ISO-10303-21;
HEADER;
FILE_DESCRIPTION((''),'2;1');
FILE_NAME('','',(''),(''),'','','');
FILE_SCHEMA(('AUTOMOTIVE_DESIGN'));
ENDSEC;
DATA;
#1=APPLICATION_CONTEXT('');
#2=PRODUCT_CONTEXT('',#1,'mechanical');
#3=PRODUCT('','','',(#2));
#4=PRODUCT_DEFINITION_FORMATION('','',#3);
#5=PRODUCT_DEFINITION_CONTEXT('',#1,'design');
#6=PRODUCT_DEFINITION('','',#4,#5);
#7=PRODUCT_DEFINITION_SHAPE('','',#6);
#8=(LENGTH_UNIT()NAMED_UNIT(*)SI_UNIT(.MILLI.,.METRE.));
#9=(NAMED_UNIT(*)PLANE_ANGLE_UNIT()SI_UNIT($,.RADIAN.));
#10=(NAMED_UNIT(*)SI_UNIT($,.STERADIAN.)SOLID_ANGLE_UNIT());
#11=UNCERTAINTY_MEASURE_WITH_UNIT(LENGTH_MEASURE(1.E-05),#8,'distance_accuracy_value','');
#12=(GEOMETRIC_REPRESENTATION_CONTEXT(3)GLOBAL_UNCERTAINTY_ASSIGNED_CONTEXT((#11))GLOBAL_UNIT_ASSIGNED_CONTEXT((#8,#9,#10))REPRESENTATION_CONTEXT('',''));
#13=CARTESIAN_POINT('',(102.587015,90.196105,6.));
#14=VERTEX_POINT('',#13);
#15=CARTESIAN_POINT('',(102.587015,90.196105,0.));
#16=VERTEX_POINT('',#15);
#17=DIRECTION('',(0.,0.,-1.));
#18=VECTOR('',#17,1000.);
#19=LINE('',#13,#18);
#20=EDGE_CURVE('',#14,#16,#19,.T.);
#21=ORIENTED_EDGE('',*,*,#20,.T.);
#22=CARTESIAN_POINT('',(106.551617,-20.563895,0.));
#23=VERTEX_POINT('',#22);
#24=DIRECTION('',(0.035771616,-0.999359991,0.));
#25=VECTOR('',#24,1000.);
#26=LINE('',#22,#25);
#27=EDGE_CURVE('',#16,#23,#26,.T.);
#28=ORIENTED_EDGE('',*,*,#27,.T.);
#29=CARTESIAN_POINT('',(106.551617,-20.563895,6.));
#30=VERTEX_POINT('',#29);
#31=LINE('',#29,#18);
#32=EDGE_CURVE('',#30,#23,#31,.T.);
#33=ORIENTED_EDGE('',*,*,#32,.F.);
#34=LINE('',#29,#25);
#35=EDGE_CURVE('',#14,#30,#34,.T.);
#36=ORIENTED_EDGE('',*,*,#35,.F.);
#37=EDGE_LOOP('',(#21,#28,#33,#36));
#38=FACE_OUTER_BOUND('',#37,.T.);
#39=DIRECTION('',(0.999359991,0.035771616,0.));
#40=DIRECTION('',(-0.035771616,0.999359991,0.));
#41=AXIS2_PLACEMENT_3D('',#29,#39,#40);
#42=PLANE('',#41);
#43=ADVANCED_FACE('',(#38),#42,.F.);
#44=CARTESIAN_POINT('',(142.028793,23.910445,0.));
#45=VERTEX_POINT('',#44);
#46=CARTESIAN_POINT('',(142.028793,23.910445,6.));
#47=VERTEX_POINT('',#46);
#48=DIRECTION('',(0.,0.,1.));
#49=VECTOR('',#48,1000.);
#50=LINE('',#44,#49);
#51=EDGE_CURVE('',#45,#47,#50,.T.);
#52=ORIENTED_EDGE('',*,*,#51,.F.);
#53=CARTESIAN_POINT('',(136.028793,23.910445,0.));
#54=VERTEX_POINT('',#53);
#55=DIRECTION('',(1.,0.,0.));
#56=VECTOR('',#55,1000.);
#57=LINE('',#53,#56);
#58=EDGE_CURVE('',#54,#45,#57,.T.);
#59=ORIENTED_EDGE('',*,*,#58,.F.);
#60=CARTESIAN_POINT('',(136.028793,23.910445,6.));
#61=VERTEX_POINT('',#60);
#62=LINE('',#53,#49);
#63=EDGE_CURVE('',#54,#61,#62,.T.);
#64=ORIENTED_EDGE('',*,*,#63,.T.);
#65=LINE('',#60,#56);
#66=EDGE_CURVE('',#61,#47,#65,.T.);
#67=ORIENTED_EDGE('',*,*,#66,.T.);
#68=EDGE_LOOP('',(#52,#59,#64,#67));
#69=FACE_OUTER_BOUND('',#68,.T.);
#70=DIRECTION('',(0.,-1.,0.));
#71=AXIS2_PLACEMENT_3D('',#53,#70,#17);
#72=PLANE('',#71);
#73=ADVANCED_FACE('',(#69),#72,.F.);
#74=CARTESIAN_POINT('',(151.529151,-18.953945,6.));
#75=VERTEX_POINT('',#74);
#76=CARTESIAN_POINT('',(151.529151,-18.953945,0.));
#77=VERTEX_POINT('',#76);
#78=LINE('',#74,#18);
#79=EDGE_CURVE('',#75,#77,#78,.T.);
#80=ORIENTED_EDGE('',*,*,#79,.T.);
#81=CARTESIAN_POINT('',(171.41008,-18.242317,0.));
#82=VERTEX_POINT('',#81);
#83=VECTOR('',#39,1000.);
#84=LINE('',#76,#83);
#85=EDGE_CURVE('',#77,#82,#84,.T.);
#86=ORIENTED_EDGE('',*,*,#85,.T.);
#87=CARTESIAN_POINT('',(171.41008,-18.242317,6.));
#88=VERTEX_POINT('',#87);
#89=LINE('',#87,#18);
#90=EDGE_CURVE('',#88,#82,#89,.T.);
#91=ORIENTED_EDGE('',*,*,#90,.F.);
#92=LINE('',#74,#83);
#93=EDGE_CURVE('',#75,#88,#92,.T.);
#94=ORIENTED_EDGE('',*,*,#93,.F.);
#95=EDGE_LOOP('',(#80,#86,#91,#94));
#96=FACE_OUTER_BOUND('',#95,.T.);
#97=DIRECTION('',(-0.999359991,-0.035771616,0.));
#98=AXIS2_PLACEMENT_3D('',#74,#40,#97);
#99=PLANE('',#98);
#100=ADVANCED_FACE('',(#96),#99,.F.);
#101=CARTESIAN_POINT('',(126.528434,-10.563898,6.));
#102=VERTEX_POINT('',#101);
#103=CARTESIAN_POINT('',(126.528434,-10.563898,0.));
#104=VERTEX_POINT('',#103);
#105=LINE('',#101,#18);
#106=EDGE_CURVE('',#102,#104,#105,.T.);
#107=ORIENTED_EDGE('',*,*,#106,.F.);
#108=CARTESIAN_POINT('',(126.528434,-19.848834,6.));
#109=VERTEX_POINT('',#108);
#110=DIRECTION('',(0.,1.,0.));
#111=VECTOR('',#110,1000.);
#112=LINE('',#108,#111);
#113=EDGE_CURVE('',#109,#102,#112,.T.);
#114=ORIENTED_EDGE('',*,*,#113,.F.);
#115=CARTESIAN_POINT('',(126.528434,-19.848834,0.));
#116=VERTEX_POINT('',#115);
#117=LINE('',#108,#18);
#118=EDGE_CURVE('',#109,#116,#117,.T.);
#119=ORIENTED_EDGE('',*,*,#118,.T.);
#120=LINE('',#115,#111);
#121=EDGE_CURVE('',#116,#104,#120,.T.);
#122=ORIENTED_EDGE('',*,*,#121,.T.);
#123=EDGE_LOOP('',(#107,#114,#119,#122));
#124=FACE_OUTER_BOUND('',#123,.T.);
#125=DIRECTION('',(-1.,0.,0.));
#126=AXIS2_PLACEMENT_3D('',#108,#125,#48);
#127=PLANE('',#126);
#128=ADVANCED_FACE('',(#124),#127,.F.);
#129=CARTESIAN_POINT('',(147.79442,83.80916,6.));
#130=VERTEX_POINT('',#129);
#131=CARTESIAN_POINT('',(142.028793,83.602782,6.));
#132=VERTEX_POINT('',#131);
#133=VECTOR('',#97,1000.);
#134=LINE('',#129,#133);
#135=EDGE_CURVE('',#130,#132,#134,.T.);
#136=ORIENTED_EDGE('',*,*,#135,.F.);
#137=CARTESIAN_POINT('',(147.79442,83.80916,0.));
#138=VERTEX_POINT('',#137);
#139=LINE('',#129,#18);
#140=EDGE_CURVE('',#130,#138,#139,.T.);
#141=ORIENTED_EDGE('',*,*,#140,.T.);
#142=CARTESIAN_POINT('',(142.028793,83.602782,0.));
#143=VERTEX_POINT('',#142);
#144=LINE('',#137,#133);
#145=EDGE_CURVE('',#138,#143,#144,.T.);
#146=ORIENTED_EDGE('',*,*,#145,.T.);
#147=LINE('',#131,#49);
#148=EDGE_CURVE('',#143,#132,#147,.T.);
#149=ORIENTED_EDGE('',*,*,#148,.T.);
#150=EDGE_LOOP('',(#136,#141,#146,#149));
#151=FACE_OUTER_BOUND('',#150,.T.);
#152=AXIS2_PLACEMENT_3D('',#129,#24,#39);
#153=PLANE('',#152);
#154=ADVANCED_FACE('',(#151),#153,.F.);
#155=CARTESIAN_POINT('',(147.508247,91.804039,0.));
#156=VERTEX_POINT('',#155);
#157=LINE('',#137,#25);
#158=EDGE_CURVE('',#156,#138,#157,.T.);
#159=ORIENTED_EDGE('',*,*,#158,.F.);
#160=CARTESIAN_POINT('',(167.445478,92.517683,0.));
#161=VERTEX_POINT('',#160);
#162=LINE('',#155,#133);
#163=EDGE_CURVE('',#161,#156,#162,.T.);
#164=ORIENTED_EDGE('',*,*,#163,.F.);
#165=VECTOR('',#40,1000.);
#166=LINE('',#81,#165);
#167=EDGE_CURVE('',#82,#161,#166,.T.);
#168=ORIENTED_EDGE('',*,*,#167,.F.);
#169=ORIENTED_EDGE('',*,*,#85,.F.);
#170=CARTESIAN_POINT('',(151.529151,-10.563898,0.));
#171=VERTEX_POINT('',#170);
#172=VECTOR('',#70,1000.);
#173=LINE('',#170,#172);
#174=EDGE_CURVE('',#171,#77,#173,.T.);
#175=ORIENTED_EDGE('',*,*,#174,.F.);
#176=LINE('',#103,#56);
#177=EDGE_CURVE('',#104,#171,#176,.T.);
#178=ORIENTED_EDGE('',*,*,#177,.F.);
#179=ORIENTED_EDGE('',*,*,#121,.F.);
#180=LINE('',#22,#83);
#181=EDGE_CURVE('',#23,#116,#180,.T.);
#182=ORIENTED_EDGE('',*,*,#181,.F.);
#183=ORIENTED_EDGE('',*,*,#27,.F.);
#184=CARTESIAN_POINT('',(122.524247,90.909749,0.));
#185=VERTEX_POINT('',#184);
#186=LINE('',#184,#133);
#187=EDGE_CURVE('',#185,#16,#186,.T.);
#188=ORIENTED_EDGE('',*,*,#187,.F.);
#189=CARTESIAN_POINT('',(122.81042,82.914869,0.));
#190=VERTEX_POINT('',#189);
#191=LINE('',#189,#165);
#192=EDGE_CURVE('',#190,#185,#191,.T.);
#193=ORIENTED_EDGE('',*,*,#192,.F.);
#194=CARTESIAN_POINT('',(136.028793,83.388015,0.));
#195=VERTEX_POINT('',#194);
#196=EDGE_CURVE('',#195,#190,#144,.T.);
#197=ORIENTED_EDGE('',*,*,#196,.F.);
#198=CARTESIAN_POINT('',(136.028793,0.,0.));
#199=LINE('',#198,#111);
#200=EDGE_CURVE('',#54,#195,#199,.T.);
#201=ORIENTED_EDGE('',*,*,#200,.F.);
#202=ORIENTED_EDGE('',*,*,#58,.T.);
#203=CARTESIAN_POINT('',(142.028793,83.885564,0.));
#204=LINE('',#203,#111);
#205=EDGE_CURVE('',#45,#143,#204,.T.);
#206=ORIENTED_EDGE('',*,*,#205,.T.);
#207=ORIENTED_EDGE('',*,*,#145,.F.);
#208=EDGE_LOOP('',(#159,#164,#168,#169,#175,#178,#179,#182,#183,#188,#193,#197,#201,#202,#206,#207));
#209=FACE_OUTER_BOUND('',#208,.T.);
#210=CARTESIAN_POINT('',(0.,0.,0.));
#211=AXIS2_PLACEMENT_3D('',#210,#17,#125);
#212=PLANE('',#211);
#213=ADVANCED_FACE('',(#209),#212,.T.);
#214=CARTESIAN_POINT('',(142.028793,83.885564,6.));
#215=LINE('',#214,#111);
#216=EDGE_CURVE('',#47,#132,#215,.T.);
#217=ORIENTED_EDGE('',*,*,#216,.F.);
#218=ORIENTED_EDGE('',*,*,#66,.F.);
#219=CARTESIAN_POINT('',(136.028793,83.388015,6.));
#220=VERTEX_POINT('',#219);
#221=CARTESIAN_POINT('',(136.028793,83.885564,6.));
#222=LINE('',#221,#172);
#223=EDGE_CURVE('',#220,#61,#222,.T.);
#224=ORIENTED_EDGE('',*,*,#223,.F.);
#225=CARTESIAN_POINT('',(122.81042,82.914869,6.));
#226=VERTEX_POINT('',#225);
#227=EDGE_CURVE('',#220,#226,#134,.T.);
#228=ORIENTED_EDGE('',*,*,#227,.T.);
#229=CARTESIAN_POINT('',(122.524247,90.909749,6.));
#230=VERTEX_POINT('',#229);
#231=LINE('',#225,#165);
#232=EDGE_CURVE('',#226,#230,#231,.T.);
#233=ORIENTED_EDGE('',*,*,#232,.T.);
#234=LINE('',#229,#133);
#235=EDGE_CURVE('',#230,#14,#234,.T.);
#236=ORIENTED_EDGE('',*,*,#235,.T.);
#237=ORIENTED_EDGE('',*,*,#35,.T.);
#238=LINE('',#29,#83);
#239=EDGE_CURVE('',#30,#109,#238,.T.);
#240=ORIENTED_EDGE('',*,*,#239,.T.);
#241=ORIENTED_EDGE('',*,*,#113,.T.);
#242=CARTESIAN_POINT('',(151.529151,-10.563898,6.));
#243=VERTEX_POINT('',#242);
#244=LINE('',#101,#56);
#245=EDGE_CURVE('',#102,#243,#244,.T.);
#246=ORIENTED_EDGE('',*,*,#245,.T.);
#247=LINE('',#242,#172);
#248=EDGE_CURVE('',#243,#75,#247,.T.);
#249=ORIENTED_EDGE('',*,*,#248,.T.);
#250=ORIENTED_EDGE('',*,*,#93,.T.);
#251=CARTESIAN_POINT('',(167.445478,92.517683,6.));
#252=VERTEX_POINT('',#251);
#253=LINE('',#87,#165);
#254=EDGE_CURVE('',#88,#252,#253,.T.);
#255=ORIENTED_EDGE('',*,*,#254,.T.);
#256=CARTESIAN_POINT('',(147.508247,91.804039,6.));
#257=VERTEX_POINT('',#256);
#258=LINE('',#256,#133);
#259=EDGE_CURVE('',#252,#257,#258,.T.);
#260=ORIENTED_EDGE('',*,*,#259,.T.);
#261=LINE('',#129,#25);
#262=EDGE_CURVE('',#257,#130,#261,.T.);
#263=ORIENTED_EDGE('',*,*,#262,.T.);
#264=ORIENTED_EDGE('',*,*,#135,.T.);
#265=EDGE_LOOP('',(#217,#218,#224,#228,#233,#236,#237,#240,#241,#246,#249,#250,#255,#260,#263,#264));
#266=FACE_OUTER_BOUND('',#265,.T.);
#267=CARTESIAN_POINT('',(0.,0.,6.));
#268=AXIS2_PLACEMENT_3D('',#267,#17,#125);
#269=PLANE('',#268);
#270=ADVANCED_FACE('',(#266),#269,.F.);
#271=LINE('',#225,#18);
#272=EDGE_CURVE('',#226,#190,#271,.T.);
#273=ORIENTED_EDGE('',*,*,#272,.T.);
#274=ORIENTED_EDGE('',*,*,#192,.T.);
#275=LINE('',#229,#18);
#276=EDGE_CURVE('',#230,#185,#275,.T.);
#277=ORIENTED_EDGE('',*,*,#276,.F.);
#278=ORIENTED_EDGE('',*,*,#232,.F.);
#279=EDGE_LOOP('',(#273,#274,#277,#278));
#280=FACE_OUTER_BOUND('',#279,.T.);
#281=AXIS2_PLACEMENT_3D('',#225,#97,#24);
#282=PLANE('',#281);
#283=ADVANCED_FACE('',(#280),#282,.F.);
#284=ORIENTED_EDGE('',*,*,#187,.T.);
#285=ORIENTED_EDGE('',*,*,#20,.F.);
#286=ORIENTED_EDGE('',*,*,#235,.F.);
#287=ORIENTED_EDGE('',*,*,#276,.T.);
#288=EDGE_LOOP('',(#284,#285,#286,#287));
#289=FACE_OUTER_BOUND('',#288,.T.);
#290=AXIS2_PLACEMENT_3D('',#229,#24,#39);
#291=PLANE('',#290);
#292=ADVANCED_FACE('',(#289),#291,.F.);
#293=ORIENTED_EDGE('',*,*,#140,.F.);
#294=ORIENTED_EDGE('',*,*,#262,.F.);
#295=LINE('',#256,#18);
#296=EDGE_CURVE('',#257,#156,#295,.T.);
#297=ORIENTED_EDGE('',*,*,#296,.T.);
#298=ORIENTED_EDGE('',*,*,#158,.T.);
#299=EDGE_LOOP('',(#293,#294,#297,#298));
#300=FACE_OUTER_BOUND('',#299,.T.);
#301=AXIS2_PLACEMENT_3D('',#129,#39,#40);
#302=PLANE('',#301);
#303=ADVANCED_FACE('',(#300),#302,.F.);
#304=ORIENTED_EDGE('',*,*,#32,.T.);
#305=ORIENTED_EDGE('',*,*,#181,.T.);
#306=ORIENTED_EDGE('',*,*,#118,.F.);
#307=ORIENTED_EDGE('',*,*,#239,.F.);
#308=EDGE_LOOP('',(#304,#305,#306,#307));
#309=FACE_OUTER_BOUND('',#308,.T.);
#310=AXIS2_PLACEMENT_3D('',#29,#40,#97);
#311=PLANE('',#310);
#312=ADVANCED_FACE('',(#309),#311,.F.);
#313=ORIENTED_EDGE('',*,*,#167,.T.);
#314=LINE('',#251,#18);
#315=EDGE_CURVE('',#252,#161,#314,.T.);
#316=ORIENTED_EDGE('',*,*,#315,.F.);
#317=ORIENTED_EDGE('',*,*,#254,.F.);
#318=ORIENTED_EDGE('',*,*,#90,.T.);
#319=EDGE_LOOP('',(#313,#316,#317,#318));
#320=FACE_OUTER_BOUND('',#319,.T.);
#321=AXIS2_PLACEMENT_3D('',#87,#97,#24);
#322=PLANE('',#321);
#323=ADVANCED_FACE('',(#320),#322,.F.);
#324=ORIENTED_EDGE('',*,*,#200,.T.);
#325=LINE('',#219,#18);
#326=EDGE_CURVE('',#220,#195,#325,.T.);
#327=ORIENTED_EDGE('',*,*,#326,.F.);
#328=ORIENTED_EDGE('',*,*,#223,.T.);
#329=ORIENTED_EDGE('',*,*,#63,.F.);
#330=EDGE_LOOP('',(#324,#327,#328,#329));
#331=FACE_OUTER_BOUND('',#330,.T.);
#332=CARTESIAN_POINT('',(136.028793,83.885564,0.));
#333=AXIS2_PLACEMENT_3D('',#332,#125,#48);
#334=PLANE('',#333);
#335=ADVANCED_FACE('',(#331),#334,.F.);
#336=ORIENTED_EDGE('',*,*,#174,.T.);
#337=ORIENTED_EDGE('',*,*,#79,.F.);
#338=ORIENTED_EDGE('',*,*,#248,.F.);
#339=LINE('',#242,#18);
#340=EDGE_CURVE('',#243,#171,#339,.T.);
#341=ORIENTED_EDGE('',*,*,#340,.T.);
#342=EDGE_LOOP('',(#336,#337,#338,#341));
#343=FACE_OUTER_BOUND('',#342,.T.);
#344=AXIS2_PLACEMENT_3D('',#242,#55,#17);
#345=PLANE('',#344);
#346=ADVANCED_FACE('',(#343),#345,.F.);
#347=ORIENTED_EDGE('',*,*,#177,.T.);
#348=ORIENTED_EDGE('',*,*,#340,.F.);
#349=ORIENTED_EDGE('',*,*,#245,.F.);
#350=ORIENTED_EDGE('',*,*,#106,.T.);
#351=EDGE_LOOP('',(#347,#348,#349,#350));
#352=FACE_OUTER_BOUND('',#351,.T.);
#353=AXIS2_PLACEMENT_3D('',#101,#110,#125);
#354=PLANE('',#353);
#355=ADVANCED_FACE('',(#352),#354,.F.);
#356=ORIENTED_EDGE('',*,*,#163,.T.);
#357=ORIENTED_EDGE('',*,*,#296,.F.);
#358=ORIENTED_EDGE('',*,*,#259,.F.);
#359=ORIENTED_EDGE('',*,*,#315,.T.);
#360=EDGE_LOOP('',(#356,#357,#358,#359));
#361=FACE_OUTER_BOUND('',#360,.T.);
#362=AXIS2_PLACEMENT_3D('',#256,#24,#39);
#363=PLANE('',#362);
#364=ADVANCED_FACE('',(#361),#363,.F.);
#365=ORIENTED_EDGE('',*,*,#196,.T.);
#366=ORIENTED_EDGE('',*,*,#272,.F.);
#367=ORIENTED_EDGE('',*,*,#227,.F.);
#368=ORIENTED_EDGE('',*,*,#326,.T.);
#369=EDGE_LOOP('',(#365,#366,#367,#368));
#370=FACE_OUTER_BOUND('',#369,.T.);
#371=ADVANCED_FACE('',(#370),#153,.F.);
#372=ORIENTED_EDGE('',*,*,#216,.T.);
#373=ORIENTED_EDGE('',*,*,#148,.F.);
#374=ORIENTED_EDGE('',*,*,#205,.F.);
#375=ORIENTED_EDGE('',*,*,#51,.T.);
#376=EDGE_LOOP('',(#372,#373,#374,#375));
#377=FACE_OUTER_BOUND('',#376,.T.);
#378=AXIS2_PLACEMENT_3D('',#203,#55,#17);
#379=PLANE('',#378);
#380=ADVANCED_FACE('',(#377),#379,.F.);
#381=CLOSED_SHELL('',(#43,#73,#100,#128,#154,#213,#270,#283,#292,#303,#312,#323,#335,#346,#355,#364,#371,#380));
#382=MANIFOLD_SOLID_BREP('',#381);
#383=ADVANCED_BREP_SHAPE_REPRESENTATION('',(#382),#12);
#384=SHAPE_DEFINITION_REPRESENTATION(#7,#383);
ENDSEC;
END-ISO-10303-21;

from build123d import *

# Parameters (mm, degrees)
BOSS_EXTRUDE1_DEPTH = 6
SKETCH2_W           = 6
SKETCH2_H           = 59.975118876
CUT_EXTRUDE1_DEPTH  = 6


with BuildPart() as part:
    # Sketch1 → Boss-Extrude1 (new body)
    with BuildSketch(Plane.XY):
        Polygon((106.551616656, -20.563894675), (102.587015051, 90.196105325), (122.52424687, 90.909749071), (122.810419801, 82.914869143), (147.794419574, 83.809159551), (147.508246643, 91.804039479), (167.445478462, 92.517683224), (171.410080068, -18.242316776), (151.529151094, -18.953945188), (151.529151094, -10.563897816), (126.528434018, -10.563897816), (126.528434018, -19.848833984), align=None)
    extrude(amount=BOSS_EXTRUDE1_DEPTH)

    # Sketch2 → Cut-Extrude1 (cut)
    with BuildSketch(Plane.XY.offset(6)):
        with Locations((139.028792556, 53.898004923)):
            Rectangle(SKETCH2_W, SKETCH2_H)
    extrude(amount=-CUT_EXTRUDE1_DEPTH, mode=Mode.SUBTRACT)


solid = part.part
